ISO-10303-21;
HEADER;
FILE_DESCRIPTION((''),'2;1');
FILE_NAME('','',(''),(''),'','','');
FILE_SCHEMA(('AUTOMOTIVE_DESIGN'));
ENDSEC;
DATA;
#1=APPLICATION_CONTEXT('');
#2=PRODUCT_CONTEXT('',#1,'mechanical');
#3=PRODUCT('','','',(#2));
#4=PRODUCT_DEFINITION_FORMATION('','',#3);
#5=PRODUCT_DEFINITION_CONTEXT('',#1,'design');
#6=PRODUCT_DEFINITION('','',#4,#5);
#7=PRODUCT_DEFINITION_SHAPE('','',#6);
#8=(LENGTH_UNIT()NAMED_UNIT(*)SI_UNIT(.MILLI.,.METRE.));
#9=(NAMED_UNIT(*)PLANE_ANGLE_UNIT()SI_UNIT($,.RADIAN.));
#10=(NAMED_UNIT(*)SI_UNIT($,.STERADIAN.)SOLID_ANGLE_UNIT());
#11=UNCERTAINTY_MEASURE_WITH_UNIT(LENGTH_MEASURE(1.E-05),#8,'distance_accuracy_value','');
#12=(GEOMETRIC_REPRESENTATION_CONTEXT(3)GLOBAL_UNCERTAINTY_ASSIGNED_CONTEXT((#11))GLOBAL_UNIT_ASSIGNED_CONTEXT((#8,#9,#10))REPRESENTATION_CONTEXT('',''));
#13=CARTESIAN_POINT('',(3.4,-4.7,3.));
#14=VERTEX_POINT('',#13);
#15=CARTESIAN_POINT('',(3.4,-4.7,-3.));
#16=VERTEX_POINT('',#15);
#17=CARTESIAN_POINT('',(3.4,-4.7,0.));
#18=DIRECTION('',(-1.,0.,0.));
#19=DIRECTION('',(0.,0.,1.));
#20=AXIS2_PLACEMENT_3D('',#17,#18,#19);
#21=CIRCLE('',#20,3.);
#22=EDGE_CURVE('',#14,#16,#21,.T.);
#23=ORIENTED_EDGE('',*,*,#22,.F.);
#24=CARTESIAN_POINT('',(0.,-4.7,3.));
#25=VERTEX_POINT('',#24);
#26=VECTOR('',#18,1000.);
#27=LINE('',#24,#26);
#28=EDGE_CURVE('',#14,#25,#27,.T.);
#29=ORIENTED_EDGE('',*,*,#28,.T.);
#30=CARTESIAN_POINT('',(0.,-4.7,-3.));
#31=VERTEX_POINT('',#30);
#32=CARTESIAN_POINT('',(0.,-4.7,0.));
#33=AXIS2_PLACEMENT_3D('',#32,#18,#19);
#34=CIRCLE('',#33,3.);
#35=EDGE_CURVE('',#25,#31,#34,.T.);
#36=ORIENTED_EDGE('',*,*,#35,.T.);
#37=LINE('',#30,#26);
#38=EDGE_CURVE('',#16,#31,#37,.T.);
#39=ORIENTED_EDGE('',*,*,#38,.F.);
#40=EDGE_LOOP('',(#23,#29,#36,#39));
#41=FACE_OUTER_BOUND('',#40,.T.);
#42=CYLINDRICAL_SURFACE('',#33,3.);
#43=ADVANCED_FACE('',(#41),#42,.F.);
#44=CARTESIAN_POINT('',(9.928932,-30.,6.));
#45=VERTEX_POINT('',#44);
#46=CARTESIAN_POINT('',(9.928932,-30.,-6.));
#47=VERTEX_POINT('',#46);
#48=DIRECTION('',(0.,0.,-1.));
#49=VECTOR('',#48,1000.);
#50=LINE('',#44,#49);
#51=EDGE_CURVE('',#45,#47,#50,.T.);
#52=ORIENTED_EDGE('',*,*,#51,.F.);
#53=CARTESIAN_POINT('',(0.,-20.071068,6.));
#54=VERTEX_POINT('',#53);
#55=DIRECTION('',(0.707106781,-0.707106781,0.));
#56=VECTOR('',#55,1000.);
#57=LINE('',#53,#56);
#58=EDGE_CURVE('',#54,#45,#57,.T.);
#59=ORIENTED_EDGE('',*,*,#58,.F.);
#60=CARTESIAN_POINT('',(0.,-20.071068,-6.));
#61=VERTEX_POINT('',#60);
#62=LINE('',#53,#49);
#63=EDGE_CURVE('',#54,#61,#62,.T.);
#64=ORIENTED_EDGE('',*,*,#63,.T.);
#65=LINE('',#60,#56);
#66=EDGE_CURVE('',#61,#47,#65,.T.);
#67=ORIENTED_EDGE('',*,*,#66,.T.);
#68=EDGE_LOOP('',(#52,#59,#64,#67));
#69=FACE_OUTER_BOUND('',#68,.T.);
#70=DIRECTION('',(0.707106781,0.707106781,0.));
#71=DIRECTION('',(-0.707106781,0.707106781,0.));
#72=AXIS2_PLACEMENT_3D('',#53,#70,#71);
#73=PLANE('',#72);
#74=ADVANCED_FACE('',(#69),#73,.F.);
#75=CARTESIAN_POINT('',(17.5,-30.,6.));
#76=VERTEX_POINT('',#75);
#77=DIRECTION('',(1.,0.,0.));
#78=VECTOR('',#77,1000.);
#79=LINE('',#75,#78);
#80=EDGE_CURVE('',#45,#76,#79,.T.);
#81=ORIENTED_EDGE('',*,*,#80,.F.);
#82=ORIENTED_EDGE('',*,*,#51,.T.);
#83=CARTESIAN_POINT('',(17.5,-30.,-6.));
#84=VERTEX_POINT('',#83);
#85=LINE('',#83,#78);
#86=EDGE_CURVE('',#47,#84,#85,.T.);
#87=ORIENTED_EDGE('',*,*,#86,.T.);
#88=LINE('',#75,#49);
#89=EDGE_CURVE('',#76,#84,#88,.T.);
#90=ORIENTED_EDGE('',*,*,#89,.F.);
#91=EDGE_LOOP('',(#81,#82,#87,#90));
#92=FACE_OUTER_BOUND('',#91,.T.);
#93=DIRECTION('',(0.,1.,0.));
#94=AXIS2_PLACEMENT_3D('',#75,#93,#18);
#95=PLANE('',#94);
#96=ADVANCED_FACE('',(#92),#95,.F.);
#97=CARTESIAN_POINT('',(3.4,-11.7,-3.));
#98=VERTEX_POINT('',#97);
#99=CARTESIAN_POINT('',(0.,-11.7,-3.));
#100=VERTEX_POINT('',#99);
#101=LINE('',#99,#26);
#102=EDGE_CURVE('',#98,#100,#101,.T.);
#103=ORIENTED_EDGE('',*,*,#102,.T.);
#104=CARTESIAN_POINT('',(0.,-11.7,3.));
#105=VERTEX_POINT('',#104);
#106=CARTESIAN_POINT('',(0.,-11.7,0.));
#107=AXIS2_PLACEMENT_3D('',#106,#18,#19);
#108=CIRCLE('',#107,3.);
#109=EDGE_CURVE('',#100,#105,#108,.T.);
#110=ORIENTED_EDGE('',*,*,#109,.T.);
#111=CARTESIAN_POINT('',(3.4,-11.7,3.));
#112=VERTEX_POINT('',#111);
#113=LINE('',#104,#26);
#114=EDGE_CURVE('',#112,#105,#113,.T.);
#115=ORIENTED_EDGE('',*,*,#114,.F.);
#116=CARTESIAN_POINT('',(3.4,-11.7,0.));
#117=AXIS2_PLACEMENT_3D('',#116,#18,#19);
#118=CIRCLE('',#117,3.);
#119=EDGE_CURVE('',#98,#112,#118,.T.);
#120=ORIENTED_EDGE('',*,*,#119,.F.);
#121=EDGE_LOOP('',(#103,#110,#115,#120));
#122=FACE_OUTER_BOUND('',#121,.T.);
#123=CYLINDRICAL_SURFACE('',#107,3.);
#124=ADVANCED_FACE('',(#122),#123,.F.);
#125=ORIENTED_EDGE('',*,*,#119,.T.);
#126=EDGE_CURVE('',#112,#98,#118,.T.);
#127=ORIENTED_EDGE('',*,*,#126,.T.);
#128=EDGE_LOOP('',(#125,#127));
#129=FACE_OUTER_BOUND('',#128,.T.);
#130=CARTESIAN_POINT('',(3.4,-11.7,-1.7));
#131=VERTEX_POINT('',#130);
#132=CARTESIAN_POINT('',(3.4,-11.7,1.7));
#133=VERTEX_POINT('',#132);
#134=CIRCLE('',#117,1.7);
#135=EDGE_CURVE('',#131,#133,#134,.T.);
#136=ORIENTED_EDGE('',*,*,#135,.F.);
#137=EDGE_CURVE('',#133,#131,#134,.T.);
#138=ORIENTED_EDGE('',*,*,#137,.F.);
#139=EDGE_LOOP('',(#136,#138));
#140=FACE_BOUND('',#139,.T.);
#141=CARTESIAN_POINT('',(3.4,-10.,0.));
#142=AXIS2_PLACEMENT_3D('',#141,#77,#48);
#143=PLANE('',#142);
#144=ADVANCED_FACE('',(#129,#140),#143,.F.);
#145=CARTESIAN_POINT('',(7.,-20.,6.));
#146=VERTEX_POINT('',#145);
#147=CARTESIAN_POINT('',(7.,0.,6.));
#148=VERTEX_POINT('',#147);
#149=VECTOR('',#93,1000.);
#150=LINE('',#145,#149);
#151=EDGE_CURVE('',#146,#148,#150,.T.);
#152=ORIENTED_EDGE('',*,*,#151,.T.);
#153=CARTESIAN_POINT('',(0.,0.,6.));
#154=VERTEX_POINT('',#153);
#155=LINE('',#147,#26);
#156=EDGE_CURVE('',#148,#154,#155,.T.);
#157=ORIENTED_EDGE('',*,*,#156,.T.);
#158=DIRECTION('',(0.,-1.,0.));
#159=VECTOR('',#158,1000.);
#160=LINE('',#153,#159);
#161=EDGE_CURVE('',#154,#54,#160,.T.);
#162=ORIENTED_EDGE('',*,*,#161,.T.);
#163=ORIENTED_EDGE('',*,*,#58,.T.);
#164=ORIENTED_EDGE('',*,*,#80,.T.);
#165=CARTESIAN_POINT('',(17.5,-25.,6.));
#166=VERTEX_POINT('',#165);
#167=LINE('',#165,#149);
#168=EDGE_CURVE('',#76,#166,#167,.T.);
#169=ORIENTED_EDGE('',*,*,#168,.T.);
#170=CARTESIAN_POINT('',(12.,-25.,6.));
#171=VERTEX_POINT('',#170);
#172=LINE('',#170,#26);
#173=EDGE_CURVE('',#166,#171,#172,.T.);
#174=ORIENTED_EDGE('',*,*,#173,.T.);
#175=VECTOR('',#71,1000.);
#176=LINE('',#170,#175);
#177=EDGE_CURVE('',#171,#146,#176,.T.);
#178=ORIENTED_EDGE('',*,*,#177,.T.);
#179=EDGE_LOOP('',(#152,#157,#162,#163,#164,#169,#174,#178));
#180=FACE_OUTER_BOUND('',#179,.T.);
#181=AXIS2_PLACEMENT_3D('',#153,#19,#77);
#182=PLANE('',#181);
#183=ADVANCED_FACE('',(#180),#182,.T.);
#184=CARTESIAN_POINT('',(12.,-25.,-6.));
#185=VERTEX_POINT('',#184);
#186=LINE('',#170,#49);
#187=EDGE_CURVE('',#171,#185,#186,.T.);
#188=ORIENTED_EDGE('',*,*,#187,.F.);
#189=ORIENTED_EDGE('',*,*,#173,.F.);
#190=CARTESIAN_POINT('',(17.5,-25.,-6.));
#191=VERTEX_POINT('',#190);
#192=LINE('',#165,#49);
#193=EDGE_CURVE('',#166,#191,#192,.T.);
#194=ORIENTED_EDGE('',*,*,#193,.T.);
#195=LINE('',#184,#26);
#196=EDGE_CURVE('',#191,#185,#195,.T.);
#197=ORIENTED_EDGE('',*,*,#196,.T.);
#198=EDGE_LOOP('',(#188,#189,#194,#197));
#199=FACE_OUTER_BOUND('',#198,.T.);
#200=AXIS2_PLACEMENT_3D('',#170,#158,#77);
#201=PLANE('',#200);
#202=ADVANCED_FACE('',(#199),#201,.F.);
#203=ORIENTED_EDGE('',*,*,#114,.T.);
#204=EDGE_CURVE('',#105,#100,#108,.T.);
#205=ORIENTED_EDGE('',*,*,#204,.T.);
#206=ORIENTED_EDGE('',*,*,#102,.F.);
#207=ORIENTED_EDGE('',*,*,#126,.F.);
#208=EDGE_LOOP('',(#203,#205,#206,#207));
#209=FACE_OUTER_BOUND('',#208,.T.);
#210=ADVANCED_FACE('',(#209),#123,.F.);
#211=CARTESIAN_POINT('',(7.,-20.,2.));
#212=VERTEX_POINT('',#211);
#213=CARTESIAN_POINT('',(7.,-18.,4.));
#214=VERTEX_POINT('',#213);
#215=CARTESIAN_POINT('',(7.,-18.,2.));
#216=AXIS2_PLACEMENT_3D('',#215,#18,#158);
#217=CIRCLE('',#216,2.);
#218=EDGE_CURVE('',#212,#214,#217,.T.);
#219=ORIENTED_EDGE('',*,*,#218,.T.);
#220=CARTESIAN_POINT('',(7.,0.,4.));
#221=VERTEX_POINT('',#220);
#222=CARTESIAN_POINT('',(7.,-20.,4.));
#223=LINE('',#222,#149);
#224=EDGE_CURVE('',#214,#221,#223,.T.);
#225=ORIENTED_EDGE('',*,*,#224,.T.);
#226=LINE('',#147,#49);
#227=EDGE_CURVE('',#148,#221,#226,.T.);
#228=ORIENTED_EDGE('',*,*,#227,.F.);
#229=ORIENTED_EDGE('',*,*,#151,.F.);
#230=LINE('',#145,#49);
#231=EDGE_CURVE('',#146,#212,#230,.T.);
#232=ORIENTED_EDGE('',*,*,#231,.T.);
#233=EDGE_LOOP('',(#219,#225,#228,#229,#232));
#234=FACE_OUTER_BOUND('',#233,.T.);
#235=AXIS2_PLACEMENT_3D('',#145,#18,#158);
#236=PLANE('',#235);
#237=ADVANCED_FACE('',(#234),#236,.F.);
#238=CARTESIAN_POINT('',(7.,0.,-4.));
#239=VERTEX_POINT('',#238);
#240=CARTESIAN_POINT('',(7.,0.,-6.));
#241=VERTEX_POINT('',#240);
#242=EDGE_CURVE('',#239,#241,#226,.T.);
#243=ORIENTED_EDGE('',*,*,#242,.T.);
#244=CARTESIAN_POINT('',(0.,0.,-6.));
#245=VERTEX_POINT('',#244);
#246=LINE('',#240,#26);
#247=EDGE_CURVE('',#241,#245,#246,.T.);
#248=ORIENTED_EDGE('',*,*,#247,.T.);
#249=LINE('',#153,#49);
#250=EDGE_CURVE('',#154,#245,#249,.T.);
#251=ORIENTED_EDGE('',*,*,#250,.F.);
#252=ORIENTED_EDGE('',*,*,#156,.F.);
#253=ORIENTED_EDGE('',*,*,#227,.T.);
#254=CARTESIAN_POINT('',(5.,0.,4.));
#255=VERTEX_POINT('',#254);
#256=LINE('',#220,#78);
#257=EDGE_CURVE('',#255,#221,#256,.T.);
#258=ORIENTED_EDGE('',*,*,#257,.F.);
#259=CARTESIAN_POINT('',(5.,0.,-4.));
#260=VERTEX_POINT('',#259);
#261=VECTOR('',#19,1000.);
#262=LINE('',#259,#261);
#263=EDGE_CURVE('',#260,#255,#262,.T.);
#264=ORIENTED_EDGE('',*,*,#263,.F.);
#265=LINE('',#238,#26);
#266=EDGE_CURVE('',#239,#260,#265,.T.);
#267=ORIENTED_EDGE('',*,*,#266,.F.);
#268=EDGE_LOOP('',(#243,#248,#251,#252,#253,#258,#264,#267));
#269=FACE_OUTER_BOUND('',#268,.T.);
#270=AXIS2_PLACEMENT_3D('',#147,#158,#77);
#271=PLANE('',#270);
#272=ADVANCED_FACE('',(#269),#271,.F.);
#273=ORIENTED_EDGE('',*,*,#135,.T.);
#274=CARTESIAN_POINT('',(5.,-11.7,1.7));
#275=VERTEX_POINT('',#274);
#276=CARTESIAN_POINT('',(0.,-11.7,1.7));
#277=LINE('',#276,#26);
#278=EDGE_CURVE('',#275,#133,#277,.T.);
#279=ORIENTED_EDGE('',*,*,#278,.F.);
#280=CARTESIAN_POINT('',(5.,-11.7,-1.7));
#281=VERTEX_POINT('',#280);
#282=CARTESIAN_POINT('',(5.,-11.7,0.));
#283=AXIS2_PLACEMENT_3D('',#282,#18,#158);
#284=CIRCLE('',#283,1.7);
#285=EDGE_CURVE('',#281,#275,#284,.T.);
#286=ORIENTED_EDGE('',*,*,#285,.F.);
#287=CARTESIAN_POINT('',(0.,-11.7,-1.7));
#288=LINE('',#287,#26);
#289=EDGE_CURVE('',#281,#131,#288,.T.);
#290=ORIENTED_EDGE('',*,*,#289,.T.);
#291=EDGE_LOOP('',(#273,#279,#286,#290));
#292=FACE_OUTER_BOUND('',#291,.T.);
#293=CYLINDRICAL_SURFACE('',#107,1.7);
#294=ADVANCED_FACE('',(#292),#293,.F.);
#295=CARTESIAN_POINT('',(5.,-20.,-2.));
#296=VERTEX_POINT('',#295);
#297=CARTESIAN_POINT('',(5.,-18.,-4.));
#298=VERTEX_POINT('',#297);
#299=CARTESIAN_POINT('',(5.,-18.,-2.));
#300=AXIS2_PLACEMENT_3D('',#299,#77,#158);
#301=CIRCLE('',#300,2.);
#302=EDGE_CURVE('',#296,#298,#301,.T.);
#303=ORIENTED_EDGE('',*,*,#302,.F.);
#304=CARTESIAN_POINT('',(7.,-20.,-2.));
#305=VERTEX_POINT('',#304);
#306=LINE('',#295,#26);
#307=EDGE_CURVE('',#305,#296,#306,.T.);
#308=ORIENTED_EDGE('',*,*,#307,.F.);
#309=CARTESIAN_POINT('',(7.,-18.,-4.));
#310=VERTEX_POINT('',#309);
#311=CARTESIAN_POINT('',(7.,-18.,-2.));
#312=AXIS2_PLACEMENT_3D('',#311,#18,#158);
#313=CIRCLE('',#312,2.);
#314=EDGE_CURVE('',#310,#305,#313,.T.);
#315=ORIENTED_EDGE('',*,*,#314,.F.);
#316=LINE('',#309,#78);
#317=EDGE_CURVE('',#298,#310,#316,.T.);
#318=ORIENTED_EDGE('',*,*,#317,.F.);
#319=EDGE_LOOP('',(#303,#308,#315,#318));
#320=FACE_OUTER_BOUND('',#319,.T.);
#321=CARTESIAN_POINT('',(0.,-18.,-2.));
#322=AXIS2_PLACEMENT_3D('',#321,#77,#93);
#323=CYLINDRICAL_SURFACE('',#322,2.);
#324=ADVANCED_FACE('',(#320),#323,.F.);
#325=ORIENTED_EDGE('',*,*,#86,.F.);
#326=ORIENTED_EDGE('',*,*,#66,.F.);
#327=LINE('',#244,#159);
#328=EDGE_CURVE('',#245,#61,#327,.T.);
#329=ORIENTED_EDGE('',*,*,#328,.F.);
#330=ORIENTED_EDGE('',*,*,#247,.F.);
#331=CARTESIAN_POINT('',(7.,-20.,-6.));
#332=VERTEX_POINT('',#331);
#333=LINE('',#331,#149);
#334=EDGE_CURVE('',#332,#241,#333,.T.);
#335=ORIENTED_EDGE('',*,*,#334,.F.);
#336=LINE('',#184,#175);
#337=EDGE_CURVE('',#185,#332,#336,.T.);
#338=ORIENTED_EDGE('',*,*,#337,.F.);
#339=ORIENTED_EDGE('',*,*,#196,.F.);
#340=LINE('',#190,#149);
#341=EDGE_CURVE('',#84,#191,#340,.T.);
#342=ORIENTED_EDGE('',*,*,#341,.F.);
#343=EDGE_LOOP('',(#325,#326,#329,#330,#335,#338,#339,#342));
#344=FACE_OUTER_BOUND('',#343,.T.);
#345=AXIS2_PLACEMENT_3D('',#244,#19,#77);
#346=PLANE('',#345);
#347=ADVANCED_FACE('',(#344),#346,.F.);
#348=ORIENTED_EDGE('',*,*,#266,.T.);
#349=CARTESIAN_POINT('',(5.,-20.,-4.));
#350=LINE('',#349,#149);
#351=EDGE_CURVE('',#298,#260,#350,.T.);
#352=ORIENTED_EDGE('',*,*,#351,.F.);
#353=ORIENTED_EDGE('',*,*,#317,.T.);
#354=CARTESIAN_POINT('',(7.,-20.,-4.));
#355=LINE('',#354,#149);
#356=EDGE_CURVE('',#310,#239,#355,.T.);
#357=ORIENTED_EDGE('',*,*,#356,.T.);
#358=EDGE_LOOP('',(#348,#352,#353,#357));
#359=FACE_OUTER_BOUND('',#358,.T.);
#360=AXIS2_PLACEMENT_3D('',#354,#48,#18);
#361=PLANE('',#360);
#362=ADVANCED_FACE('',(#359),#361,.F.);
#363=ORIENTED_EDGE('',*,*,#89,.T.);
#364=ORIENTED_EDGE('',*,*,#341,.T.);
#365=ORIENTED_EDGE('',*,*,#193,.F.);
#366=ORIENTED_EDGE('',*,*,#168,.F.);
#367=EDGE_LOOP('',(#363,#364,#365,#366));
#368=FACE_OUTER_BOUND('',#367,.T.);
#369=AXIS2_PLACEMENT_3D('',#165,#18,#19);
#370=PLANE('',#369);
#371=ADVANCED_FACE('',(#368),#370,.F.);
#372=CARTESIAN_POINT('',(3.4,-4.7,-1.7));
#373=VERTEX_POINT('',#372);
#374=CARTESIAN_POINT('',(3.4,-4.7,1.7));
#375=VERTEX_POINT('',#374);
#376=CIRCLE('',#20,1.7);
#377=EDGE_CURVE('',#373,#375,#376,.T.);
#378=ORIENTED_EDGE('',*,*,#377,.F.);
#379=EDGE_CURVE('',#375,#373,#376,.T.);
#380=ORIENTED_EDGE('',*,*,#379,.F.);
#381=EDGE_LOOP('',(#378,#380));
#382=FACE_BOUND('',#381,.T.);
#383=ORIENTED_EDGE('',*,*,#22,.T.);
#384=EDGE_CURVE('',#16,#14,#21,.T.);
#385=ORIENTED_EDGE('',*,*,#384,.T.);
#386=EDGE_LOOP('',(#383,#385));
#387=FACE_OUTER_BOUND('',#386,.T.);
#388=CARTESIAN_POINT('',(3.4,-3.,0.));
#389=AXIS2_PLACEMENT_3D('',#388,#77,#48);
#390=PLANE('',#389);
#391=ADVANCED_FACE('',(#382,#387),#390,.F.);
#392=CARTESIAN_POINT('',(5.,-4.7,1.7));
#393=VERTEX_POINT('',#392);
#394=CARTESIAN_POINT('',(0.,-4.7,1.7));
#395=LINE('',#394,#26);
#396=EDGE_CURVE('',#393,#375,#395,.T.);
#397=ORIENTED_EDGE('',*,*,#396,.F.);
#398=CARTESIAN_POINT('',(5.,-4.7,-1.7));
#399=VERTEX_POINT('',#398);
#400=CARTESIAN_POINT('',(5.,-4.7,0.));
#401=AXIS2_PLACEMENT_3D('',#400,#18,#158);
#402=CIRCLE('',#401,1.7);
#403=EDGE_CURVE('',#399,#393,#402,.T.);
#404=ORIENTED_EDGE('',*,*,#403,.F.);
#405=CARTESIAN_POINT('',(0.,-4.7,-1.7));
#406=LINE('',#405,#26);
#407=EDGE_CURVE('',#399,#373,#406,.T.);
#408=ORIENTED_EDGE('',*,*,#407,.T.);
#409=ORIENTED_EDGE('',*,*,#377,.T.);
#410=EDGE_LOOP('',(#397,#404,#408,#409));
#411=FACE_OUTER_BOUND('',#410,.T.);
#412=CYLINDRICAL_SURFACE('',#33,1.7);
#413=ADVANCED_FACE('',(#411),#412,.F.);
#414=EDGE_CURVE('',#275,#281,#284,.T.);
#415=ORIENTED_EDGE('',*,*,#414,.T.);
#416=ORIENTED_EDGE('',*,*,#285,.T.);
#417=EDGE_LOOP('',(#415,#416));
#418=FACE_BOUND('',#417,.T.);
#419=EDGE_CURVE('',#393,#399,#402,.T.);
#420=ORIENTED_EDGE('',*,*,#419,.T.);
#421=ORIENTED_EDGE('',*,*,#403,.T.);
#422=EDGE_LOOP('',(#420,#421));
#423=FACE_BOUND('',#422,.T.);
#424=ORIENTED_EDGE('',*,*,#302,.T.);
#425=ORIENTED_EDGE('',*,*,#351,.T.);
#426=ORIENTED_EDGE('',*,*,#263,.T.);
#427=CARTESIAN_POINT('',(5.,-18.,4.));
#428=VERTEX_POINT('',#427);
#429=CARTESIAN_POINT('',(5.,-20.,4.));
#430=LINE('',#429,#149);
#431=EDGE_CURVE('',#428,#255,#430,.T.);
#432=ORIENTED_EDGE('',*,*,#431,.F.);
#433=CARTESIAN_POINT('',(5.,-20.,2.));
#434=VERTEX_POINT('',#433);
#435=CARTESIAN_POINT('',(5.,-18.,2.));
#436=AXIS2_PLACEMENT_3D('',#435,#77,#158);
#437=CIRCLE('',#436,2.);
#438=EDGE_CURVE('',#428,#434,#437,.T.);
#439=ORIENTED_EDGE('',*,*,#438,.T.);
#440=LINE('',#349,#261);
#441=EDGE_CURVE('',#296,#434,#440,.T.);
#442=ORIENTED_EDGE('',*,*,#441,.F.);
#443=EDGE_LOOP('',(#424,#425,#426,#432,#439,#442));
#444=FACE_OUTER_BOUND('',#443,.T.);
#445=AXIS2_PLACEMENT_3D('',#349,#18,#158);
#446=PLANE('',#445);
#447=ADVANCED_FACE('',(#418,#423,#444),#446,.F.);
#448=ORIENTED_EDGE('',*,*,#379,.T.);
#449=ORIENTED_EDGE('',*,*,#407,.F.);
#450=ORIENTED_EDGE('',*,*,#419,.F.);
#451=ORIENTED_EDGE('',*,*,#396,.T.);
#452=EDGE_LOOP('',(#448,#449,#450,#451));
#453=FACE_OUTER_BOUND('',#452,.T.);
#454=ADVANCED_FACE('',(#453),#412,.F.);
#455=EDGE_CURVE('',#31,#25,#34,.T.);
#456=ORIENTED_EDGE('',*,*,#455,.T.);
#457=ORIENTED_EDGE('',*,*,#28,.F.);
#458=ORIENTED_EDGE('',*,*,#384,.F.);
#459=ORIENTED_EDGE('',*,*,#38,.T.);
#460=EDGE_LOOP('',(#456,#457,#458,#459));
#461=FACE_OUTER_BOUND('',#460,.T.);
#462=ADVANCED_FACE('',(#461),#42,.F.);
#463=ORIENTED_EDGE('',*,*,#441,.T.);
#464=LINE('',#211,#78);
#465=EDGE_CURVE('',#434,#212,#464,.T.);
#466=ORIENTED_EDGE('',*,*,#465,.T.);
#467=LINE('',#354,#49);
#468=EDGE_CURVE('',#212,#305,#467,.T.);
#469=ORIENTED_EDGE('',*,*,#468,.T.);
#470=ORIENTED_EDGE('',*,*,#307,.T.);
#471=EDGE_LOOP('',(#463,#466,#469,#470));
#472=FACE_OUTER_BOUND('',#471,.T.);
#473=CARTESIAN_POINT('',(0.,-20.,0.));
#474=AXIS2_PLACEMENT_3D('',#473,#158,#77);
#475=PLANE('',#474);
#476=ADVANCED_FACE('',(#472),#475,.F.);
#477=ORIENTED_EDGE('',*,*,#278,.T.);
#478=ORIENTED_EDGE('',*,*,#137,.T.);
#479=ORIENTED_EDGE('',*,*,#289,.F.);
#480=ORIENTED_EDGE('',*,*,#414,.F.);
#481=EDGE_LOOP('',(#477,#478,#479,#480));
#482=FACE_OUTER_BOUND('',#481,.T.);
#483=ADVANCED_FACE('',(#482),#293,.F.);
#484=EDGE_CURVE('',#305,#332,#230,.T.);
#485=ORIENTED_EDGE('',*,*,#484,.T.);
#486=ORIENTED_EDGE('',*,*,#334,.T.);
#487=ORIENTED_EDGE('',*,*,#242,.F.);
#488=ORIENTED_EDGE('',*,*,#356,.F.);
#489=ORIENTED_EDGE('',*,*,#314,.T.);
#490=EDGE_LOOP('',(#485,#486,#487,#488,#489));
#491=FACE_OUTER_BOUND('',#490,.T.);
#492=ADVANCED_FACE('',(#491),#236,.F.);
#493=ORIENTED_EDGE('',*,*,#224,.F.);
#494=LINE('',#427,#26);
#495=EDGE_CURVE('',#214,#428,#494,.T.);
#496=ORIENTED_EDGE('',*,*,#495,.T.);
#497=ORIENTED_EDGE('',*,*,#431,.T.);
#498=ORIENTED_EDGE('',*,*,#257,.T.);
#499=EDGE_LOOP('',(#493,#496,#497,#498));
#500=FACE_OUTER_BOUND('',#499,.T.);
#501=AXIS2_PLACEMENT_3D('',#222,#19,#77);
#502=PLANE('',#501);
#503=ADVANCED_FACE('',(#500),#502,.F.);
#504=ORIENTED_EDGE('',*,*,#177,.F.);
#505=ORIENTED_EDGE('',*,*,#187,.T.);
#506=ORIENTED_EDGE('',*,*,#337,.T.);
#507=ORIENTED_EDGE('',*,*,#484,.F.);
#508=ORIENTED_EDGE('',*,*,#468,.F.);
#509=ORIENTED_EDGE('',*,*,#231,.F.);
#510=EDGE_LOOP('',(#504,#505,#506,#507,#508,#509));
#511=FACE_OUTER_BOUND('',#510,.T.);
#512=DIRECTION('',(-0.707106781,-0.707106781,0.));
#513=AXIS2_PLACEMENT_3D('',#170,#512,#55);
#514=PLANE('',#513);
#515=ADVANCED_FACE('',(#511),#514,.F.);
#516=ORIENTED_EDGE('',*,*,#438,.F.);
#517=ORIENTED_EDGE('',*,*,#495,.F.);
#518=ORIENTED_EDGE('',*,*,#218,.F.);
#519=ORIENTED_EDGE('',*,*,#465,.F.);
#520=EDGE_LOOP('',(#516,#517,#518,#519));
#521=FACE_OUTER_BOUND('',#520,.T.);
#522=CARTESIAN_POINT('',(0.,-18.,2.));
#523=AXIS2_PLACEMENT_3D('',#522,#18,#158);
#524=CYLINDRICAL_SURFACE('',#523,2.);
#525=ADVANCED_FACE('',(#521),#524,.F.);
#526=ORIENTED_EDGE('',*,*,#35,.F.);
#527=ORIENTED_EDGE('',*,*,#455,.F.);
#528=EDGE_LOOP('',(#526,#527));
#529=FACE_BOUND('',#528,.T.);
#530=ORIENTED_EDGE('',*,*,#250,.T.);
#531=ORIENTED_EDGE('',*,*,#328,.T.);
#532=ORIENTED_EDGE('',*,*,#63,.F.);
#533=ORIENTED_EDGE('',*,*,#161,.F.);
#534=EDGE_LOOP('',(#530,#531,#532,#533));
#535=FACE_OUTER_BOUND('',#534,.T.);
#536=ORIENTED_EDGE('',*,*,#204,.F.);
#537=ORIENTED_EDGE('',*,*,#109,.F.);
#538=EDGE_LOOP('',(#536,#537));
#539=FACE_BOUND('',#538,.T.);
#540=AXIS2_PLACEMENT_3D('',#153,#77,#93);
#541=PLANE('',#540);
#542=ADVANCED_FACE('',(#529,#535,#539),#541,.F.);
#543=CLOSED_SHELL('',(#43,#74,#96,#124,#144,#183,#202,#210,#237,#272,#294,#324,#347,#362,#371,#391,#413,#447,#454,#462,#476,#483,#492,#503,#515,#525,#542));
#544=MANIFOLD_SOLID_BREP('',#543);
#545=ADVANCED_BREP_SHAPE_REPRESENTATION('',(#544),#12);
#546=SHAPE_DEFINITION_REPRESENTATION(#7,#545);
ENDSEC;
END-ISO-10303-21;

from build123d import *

# Parameters (mm, degrees)
EXTRUDE_1_DEPTH              = 6
SKETCH_2_W                   = 2
SKETCH_2_H                   = 8
CUT_EXTRUDE_1_DEPTH          = 20
FILLET_1_R                   = 2
HOLE_WIZARD_M3_1_D           = 3.4
HOLE_WIZARD_M3_1_CBORE_D     = 6
HOLE_WIZARD_M3_1_CBORE_DEPTH = 3.4


with BuildPart() as part:
    # 草图1 → 凸台-拉伸1 (new, symmetric)
    with BuildSketch(Plane.XY):
        Polygon((0, 0), (0, -20.071067812), (9.928932188, -30), (17.5, -30), (17.5, -25), (12, -25), (7, -20), (7, 0), align=None)
    extrude(amount=EXTRUDE_1_DEPTH, both=True)

    # 草图2 → 切除-拉伸1 (cut)
    with BuildSketch(Plane(origin=(0, 0, 0), x_dir=(1, 0, 0), z_dir=(0, 1, 0))):
        with Locations((6, 0)):
            Rectangle(SKETCH_2_W, SKETCH_2_H)
    extrude(amount=-CUT_EXTRUDE_1_DEPTH, mode=Mode.SUBTRACT)

    # 圆角1
    fillet_1_edges = [part.edges().sort_by_distance(p)[0] for p in [
        (6, -20, -4),
        (6, -20, 4),
    ]]
    fillet(fillet_1_edges, radius=FILLET_1_R)

    # M3 六角圆柱头螺钉的柱形沉头孔1 (through all)
    with Locations(Plane.ZY):
        with Locations((0, -4.7), (0, -11.7)):
            CounterBoreHole(HOLE_WIZARD_M3_1_D / 2, HOLE_WIZARD_M3_1_CBORE_D / 2, HOLE_WIZARD_M3_1_CBORE_DEPTH)


solid = part.part
